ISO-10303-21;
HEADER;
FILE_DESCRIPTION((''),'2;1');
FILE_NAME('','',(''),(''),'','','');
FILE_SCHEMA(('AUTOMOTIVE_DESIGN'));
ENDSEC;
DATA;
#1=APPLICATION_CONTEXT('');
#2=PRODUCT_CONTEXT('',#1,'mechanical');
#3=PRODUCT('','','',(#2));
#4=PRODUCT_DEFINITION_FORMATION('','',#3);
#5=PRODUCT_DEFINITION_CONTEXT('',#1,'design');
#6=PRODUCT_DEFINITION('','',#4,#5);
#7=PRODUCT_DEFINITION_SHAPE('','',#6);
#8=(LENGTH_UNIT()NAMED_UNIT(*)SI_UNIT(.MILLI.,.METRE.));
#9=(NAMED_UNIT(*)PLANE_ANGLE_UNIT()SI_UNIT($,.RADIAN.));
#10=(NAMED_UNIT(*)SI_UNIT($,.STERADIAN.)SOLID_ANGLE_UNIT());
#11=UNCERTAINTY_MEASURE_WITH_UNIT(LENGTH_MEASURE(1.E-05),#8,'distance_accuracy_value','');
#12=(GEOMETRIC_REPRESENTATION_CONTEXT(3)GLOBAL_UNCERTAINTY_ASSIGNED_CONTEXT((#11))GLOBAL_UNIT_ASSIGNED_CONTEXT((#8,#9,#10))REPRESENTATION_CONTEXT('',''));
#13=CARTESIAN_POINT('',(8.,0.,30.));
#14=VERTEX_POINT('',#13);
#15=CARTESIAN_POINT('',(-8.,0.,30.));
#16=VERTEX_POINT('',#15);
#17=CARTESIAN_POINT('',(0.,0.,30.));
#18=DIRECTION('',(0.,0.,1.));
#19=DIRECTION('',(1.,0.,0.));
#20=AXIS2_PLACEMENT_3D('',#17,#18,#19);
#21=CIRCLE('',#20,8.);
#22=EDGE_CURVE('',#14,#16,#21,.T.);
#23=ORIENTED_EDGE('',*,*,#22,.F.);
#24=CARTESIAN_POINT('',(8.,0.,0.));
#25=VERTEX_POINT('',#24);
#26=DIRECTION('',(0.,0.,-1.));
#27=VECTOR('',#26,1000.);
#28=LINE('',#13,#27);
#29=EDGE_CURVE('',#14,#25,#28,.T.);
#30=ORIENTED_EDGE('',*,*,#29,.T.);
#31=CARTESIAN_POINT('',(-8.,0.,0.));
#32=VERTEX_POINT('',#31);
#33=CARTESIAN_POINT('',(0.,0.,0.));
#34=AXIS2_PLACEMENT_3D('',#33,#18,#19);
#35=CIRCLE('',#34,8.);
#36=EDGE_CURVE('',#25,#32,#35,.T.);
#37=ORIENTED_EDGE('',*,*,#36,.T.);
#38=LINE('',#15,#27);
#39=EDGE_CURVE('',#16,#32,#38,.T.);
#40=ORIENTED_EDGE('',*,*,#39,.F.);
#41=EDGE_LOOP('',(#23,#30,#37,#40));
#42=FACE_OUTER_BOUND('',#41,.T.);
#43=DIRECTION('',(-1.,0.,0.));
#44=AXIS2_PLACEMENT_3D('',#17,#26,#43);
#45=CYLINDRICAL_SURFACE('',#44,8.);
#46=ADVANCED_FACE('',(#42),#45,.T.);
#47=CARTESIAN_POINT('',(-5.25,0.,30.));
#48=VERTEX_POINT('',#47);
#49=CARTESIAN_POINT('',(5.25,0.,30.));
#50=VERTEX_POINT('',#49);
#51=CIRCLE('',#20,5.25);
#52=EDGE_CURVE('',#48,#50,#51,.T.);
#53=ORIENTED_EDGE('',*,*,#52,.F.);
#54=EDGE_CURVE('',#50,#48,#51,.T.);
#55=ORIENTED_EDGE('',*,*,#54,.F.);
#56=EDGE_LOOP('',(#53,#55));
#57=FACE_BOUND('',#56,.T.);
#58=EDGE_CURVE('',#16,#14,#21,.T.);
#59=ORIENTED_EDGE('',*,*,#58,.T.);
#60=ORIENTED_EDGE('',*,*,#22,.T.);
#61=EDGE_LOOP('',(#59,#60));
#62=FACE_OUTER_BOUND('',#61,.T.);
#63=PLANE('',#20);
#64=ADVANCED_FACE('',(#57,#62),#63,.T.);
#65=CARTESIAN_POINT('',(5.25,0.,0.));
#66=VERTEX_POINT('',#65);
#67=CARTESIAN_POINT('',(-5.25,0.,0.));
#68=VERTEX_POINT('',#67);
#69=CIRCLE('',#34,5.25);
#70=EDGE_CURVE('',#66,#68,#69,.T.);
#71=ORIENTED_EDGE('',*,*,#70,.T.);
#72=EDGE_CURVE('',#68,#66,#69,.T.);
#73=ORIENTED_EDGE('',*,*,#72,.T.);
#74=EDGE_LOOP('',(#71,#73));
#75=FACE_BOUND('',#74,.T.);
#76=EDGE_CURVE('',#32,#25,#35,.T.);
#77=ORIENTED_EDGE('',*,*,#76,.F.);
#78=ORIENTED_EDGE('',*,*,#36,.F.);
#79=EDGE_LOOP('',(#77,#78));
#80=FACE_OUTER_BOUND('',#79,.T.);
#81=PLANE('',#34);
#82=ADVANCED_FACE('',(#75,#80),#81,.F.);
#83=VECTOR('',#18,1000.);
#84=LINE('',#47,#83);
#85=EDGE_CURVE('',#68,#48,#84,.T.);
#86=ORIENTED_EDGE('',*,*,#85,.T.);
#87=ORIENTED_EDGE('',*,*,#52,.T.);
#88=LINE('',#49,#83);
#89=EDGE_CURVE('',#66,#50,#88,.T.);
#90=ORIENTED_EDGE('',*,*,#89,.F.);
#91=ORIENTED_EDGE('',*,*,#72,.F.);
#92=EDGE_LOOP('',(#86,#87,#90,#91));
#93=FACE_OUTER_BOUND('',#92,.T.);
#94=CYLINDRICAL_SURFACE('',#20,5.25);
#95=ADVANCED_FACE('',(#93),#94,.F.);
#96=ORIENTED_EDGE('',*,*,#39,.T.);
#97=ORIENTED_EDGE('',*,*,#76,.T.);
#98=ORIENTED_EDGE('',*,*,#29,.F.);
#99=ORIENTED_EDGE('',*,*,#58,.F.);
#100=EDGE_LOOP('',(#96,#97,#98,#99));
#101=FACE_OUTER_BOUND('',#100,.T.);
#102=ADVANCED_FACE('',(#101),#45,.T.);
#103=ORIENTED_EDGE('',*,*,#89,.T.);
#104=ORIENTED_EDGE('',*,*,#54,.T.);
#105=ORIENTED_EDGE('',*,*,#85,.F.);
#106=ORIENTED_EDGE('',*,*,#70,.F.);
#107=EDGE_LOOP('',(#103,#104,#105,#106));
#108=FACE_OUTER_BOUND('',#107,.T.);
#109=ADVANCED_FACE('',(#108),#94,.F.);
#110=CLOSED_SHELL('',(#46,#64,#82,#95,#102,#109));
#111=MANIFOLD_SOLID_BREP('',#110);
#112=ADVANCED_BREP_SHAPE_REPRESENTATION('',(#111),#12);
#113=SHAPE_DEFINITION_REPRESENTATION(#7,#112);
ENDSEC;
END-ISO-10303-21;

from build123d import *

# Parameters (mm, degrees)
SKETCH1_R                   = 8
BOSS_EXTRUDE1_DEPTH         = 30
M12X1_25_TAPPED_HOLE1_D     = 10.5
M12X1_25_TAPPED_HOLE1_DEPTH = 30
M12X1_25_TAPPED_HOLE1_TIP   = 3.15451825


with BuildPart() as part:
    # Sketch1 → Boss-Extrude1 (new body)
    with BuildSketch(Plane.XY):
        Circle(SKETCH1_R)
    extrude(amount=BOSS_EXTRUDE1_DEPTH)

    # M12x1.25 Tapped Hole1
    with Locations(Plane.XY.offset(30)):
        with Locations((0, 0)):
            Hole(M12X1_25_TAPPED_HOLE1_D / 2, depth=M12X1_25_TAPPED_HOLE1_DEPTH)
            with Locations((0, 0, -(M12X1_25_TAPPED_HOLE1_DEPTH + M12X1_25_TAPPED_HOLE1_TIP / 2))):  # 118° drill point
                Cone(0, M12X1_25_TAPPED_HOLE1_D / 2, M12X1_25_TAPPED_HOLE1_TIP, mode=Mode.SUBTRACT)


solid = part.part
